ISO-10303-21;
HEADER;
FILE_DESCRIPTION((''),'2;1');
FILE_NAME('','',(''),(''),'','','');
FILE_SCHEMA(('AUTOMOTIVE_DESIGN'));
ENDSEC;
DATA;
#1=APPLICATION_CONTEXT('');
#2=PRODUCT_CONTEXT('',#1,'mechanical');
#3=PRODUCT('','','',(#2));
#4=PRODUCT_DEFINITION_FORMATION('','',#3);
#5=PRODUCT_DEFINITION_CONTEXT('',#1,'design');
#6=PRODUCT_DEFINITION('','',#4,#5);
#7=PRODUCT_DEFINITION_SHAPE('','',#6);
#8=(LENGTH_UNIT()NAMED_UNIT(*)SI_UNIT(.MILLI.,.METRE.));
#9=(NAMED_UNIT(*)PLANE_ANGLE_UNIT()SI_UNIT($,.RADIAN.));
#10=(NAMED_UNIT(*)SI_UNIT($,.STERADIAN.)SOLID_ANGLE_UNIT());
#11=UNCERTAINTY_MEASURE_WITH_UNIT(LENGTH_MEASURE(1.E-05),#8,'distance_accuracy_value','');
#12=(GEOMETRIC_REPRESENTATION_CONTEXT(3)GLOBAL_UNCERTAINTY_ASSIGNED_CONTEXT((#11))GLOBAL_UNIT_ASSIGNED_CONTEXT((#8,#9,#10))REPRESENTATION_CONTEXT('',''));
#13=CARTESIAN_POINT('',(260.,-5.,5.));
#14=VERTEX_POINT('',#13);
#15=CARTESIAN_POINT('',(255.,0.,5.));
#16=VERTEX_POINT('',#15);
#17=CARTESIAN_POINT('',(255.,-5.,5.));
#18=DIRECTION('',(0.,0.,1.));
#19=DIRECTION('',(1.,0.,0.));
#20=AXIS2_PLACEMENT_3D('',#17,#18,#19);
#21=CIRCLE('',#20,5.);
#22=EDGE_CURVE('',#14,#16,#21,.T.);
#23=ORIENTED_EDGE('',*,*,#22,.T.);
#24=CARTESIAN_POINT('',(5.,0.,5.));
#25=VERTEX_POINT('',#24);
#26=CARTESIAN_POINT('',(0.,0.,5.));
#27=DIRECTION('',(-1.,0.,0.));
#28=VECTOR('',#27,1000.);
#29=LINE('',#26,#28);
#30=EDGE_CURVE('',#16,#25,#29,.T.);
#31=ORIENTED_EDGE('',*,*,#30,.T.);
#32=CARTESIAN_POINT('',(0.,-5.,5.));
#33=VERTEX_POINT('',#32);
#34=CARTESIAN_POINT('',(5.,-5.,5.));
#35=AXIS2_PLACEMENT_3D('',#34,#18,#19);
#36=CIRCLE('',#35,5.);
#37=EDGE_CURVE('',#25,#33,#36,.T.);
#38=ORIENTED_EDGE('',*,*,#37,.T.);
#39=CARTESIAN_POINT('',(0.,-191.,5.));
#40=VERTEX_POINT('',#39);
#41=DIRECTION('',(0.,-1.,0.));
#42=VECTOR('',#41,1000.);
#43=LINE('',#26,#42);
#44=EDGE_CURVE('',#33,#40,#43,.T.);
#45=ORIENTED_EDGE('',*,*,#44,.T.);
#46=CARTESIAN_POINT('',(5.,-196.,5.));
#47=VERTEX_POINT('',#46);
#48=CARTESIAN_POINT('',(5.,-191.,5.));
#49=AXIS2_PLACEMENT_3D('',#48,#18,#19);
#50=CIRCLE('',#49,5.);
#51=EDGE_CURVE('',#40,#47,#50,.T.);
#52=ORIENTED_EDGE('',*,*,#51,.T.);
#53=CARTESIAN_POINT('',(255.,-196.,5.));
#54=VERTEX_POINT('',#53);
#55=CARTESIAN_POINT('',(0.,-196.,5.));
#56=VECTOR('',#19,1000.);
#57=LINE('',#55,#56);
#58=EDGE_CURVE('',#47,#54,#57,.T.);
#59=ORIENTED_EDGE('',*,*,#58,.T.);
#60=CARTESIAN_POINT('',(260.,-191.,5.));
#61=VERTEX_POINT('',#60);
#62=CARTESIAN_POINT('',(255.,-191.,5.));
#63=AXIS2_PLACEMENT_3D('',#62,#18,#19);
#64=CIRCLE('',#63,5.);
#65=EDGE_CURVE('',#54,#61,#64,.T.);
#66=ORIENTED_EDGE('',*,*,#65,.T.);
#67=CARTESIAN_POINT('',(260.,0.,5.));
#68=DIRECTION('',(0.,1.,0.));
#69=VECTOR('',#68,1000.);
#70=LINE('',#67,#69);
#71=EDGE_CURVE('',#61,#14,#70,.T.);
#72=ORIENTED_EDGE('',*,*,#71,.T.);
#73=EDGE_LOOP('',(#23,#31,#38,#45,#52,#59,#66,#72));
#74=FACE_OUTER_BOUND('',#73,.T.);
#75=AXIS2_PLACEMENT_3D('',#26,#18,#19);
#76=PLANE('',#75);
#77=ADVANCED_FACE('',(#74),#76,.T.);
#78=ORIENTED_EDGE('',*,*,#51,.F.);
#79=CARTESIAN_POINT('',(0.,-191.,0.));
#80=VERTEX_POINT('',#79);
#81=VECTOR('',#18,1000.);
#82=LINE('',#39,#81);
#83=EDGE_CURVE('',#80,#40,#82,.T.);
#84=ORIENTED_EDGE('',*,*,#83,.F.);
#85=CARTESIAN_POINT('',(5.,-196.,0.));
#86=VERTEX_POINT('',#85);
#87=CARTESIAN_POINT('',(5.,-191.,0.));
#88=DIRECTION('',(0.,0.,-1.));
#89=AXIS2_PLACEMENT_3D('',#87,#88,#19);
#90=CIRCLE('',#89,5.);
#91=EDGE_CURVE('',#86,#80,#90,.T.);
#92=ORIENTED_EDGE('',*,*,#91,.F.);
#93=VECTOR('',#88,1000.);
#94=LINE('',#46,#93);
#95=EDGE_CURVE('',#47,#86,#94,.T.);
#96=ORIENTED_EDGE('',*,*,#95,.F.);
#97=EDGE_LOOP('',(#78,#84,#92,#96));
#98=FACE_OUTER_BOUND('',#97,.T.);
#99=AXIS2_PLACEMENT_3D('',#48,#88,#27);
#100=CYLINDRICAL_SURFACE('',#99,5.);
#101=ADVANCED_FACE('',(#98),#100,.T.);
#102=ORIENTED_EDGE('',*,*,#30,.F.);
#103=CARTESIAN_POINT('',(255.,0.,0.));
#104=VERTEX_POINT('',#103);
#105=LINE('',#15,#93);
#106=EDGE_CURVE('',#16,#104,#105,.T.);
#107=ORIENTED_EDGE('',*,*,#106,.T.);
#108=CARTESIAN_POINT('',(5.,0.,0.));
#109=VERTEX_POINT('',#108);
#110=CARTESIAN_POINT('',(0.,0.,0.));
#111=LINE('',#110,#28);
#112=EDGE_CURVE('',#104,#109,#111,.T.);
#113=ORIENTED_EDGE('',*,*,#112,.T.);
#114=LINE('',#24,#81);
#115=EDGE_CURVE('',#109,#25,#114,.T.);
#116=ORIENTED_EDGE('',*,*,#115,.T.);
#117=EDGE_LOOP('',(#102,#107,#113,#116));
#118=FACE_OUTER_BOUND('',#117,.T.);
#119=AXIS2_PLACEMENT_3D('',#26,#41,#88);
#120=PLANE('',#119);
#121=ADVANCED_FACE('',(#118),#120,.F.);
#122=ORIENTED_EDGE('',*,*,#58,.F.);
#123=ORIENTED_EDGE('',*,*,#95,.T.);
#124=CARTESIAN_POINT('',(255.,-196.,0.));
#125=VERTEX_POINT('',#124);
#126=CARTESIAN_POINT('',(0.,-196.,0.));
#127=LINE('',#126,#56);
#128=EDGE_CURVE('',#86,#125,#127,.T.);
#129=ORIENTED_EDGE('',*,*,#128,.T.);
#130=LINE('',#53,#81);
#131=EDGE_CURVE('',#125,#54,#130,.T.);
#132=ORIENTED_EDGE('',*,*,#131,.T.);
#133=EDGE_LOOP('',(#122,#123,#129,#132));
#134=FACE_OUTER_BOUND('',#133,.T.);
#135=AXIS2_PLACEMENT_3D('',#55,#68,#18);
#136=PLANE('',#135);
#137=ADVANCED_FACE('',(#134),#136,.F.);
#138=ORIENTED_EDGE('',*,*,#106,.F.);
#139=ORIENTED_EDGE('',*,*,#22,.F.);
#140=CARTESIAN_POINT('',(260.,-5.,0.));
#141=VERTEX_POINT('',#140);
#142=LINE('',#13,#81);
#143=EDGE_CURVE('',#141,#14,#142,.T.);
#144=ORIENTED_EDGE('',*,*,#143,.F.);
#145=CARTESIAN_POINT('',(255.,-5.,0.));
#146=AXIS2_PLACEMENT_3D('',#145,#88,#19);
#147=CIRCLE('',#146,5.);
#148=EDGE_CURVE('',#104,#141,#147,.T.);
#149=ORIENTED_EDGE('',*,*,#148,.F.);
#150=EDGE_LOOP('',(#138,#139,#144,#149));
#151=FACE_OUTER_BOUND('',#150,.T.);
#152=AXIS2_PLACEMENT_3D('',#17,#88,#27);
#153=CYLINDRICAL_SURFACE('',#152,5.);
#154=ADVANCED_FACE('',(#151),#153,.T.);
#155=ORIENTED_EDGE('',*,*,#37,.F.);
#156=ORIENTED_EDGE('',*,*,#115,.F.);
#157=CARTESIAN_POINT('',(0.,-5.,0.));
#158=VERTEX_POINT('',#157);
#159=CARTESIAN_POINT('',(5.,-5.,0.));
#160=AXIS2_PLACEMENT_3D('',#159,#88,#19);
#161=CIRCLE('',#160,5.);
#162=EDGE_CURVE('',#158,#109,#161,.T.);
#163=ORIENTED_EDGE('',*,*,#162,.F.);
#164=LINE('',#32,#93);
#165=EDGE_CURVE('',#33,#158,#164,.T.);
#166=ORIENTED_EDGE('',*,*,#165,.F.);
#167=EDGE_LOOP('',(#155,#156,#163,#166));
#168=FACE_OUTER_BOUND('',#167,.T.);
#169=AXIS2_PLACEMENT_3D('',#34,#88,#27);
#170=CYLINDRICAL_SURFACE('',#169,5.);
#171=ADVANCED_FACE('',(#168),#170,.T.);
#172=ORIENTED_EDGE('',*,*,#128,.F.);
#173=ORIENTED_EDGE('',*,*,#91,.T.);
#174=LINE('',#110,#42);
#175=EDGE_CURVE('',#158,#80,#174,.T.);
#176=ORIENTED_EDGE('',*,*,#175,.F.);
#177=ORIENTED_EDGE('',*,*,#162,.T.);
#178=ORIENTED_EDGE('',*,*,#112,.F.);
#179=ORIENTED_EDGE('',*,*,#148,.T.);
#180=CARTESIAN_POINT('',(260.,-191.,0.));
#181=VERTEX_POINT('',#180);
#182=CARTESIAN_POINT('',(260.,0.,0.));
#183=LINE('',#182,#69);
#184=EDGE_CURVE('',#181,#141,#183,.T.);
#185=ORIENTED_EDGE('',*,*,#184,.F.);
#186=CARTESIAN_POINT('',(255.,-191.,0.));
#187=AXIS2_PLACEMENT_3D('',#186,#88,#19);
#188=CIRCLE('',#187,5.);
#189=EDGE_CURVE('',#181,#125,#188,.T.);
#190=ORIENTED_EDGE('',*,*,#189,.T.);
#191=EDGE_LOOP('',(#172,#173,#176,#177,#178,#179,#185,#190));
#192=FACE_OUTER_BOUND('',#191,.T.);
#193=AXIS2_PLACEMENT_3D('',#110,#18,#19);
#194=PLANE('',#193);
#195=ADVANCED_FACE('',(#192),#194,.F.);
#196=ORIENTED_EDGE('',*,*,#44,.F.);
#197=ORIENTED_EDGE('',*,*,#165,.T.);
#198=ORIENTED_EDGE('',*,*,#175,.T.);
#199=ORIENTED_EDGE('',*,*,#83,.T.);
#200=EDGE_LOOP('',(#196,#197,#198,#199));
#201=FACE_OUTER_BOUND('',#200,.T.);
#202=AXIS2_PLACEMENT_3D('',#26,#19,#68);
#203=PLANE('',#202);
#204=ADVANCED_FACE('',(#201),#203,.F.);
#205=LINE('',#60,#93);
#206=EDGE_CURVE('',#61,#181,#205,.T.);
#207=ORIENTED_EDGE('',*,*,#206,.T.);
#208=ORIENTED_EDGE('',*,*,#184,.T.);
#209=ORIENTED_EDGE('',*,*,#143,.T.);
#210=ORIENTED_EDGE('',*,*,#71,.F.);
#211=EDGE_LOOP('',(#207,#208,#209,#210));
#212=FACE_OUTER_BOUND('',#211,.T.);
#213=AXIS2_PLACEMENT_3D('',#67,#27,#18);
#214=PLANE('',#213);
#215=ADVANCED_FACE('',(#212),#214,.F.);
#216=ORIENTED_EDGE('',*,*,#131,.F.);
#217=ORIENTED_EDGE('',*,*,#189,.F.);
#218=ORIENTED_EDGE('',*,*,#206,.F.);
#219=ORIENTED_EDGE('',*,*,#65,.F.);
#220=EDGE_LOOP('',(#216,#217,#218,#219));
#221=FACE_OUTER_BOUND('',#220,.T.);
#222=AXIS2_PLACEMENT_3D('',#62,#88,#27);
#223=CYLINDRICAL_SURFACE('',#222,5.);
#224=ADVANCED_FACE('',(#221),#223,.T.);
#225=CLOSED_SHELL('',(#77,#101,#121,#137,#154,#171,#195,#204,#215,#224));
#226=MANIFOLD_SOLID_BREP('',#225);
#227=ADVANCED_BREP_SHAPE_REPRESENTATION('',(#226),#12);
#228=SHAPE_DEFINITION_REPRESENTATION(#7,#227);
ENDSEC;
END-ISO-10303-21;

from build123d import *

# Parameters (mm, degrees)
SKETCH1_W           = 260
SKETCH1_H           = 196
BOSS_EXTRUDE1_DEPTH = 5
FILLET1_R           = 5


with BuildPart() as part:
    # Sketch1 → Boss-Extrude1 (new body)
    with BuildSketch(Plane.XY):
        with Locations((130, -98)):
            Rectangle(SKETCH1_W, SKETCH1_H)
    extrude(amount=BOSS_EXTRUDE1_DEPTH)

    # Fillet1
    fillet1_edges = [part.edges().sort_by_distance(p)[0] for p in [
        (0, 0, 2.5),
        (260, 0, 2.5),
        (260, -196, 2.5),
        (0, -196, 2.5),
    ]]
    fillet(fillet1_edges, radius=FILLET1_R)


solid = part.part
